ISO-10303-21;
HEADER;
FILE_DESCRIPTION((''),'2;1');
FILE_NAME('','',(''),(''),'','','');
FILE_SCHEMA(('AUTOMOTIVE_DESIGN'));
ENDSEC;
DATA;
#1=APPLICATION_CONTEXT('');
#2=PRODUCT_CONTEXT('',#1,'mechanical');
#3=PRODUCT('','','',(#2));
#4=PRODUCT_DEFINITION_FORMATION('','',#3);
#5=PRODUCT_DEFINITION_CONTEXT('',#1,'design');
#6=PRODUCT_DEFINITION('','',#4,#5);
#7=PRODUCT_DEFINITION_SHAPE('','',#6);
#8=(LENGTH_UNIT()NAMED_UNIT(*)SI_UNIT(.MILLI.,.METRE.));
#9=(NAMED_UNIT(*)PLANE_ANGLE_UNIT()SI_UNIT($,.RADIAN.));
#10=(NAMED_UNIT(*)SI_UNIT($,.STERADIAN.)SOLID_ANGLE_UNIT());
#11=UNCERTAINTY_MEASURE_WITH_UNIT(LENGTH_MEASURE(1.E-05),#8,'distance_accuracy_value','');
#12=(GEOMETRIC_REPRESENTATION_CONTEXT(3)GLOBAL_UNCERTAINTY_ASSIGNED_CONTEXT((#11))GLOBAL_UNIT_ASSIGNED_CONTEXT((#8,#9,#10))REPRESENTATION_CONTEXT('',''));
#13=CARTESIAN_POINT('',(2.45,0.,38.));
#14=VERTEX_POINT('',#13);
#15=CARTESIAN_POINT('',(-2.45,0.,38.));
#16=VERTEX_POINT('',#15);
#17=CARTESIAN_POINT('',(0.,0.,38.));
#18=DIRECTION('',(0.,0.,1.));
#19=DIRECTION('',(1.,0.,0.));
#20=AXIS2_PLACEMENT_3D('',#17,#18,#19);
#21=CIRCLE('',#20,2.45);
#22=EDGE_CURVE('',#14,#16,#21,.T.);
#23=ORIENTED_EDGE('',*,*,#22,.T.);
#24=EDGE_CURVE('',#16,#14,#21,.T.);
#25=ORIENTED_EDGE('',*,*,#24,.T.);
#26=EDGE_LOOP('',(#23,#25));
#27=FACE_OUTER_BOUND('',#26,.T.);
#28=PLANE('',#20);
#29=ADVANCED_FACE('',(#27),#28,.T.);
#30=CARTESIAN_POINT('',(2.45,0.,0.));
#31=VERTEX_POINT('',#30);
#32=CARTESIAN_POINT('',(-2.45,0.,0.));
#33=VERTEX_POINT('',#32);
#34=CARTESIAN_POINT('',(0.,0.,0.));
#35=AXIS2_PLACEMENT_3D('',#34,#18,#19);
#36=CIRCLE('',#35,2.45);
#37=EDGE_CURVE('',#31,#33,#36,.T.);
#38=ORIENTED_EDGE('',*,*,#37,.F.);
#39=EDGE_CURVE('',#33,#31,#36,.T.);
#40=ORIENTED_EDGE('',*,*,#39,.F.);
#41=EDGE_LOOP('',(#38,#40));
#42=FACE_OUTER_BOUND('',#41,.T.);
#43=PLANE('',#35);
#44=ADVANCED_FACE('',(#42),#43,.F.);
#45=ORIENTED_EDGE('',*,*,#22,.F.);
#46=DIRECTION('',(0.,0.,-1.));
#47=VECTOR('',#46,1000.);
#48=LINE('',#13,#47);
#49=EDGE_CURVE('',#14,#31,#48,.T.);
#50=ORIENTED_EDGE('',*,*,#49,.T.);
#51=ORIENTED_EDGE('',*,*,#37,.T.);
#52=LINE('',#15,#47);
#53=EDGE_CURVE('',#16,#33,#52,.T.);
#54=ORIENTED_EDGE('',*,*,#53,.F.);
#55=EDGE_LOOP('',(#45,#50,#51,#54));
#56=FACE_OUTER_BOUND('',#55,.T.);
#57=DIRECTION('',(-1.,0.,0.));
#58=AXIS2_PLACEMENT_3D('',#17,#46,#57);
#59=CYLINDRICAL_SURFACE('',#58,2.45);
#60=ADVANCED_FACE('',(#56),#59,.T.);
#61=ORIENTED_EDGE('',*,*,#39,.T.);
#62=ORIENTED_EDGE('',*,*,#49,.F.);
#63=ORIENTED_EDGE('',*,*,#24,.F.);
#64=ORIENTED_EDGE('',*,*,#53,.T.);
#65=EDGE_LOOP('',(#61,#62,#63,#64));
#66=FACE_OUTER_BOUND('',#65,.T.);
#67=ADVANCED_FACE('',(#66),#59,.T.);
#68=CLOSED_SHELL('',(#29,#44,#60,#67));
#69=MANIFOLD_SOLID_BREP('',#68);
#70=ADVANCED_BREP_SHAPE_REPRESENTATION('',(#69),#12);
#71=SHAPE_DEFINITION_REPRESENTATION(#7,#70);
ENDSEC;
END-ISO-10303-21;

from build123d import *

# Parameters (mm, degrees)
SKETCH_1_R      = 2.45
EXTRUDE_1_DEPTH = 38


with BuildPart() as part:
    # 草图1 → 凸台-拉伸1 (new body)
    with BuildSketch(Plane.XY):
        Circle(SKETCH_1_R)
    extrude(amount=EXTRUDE_1_DEPTH)


solid = part.part
